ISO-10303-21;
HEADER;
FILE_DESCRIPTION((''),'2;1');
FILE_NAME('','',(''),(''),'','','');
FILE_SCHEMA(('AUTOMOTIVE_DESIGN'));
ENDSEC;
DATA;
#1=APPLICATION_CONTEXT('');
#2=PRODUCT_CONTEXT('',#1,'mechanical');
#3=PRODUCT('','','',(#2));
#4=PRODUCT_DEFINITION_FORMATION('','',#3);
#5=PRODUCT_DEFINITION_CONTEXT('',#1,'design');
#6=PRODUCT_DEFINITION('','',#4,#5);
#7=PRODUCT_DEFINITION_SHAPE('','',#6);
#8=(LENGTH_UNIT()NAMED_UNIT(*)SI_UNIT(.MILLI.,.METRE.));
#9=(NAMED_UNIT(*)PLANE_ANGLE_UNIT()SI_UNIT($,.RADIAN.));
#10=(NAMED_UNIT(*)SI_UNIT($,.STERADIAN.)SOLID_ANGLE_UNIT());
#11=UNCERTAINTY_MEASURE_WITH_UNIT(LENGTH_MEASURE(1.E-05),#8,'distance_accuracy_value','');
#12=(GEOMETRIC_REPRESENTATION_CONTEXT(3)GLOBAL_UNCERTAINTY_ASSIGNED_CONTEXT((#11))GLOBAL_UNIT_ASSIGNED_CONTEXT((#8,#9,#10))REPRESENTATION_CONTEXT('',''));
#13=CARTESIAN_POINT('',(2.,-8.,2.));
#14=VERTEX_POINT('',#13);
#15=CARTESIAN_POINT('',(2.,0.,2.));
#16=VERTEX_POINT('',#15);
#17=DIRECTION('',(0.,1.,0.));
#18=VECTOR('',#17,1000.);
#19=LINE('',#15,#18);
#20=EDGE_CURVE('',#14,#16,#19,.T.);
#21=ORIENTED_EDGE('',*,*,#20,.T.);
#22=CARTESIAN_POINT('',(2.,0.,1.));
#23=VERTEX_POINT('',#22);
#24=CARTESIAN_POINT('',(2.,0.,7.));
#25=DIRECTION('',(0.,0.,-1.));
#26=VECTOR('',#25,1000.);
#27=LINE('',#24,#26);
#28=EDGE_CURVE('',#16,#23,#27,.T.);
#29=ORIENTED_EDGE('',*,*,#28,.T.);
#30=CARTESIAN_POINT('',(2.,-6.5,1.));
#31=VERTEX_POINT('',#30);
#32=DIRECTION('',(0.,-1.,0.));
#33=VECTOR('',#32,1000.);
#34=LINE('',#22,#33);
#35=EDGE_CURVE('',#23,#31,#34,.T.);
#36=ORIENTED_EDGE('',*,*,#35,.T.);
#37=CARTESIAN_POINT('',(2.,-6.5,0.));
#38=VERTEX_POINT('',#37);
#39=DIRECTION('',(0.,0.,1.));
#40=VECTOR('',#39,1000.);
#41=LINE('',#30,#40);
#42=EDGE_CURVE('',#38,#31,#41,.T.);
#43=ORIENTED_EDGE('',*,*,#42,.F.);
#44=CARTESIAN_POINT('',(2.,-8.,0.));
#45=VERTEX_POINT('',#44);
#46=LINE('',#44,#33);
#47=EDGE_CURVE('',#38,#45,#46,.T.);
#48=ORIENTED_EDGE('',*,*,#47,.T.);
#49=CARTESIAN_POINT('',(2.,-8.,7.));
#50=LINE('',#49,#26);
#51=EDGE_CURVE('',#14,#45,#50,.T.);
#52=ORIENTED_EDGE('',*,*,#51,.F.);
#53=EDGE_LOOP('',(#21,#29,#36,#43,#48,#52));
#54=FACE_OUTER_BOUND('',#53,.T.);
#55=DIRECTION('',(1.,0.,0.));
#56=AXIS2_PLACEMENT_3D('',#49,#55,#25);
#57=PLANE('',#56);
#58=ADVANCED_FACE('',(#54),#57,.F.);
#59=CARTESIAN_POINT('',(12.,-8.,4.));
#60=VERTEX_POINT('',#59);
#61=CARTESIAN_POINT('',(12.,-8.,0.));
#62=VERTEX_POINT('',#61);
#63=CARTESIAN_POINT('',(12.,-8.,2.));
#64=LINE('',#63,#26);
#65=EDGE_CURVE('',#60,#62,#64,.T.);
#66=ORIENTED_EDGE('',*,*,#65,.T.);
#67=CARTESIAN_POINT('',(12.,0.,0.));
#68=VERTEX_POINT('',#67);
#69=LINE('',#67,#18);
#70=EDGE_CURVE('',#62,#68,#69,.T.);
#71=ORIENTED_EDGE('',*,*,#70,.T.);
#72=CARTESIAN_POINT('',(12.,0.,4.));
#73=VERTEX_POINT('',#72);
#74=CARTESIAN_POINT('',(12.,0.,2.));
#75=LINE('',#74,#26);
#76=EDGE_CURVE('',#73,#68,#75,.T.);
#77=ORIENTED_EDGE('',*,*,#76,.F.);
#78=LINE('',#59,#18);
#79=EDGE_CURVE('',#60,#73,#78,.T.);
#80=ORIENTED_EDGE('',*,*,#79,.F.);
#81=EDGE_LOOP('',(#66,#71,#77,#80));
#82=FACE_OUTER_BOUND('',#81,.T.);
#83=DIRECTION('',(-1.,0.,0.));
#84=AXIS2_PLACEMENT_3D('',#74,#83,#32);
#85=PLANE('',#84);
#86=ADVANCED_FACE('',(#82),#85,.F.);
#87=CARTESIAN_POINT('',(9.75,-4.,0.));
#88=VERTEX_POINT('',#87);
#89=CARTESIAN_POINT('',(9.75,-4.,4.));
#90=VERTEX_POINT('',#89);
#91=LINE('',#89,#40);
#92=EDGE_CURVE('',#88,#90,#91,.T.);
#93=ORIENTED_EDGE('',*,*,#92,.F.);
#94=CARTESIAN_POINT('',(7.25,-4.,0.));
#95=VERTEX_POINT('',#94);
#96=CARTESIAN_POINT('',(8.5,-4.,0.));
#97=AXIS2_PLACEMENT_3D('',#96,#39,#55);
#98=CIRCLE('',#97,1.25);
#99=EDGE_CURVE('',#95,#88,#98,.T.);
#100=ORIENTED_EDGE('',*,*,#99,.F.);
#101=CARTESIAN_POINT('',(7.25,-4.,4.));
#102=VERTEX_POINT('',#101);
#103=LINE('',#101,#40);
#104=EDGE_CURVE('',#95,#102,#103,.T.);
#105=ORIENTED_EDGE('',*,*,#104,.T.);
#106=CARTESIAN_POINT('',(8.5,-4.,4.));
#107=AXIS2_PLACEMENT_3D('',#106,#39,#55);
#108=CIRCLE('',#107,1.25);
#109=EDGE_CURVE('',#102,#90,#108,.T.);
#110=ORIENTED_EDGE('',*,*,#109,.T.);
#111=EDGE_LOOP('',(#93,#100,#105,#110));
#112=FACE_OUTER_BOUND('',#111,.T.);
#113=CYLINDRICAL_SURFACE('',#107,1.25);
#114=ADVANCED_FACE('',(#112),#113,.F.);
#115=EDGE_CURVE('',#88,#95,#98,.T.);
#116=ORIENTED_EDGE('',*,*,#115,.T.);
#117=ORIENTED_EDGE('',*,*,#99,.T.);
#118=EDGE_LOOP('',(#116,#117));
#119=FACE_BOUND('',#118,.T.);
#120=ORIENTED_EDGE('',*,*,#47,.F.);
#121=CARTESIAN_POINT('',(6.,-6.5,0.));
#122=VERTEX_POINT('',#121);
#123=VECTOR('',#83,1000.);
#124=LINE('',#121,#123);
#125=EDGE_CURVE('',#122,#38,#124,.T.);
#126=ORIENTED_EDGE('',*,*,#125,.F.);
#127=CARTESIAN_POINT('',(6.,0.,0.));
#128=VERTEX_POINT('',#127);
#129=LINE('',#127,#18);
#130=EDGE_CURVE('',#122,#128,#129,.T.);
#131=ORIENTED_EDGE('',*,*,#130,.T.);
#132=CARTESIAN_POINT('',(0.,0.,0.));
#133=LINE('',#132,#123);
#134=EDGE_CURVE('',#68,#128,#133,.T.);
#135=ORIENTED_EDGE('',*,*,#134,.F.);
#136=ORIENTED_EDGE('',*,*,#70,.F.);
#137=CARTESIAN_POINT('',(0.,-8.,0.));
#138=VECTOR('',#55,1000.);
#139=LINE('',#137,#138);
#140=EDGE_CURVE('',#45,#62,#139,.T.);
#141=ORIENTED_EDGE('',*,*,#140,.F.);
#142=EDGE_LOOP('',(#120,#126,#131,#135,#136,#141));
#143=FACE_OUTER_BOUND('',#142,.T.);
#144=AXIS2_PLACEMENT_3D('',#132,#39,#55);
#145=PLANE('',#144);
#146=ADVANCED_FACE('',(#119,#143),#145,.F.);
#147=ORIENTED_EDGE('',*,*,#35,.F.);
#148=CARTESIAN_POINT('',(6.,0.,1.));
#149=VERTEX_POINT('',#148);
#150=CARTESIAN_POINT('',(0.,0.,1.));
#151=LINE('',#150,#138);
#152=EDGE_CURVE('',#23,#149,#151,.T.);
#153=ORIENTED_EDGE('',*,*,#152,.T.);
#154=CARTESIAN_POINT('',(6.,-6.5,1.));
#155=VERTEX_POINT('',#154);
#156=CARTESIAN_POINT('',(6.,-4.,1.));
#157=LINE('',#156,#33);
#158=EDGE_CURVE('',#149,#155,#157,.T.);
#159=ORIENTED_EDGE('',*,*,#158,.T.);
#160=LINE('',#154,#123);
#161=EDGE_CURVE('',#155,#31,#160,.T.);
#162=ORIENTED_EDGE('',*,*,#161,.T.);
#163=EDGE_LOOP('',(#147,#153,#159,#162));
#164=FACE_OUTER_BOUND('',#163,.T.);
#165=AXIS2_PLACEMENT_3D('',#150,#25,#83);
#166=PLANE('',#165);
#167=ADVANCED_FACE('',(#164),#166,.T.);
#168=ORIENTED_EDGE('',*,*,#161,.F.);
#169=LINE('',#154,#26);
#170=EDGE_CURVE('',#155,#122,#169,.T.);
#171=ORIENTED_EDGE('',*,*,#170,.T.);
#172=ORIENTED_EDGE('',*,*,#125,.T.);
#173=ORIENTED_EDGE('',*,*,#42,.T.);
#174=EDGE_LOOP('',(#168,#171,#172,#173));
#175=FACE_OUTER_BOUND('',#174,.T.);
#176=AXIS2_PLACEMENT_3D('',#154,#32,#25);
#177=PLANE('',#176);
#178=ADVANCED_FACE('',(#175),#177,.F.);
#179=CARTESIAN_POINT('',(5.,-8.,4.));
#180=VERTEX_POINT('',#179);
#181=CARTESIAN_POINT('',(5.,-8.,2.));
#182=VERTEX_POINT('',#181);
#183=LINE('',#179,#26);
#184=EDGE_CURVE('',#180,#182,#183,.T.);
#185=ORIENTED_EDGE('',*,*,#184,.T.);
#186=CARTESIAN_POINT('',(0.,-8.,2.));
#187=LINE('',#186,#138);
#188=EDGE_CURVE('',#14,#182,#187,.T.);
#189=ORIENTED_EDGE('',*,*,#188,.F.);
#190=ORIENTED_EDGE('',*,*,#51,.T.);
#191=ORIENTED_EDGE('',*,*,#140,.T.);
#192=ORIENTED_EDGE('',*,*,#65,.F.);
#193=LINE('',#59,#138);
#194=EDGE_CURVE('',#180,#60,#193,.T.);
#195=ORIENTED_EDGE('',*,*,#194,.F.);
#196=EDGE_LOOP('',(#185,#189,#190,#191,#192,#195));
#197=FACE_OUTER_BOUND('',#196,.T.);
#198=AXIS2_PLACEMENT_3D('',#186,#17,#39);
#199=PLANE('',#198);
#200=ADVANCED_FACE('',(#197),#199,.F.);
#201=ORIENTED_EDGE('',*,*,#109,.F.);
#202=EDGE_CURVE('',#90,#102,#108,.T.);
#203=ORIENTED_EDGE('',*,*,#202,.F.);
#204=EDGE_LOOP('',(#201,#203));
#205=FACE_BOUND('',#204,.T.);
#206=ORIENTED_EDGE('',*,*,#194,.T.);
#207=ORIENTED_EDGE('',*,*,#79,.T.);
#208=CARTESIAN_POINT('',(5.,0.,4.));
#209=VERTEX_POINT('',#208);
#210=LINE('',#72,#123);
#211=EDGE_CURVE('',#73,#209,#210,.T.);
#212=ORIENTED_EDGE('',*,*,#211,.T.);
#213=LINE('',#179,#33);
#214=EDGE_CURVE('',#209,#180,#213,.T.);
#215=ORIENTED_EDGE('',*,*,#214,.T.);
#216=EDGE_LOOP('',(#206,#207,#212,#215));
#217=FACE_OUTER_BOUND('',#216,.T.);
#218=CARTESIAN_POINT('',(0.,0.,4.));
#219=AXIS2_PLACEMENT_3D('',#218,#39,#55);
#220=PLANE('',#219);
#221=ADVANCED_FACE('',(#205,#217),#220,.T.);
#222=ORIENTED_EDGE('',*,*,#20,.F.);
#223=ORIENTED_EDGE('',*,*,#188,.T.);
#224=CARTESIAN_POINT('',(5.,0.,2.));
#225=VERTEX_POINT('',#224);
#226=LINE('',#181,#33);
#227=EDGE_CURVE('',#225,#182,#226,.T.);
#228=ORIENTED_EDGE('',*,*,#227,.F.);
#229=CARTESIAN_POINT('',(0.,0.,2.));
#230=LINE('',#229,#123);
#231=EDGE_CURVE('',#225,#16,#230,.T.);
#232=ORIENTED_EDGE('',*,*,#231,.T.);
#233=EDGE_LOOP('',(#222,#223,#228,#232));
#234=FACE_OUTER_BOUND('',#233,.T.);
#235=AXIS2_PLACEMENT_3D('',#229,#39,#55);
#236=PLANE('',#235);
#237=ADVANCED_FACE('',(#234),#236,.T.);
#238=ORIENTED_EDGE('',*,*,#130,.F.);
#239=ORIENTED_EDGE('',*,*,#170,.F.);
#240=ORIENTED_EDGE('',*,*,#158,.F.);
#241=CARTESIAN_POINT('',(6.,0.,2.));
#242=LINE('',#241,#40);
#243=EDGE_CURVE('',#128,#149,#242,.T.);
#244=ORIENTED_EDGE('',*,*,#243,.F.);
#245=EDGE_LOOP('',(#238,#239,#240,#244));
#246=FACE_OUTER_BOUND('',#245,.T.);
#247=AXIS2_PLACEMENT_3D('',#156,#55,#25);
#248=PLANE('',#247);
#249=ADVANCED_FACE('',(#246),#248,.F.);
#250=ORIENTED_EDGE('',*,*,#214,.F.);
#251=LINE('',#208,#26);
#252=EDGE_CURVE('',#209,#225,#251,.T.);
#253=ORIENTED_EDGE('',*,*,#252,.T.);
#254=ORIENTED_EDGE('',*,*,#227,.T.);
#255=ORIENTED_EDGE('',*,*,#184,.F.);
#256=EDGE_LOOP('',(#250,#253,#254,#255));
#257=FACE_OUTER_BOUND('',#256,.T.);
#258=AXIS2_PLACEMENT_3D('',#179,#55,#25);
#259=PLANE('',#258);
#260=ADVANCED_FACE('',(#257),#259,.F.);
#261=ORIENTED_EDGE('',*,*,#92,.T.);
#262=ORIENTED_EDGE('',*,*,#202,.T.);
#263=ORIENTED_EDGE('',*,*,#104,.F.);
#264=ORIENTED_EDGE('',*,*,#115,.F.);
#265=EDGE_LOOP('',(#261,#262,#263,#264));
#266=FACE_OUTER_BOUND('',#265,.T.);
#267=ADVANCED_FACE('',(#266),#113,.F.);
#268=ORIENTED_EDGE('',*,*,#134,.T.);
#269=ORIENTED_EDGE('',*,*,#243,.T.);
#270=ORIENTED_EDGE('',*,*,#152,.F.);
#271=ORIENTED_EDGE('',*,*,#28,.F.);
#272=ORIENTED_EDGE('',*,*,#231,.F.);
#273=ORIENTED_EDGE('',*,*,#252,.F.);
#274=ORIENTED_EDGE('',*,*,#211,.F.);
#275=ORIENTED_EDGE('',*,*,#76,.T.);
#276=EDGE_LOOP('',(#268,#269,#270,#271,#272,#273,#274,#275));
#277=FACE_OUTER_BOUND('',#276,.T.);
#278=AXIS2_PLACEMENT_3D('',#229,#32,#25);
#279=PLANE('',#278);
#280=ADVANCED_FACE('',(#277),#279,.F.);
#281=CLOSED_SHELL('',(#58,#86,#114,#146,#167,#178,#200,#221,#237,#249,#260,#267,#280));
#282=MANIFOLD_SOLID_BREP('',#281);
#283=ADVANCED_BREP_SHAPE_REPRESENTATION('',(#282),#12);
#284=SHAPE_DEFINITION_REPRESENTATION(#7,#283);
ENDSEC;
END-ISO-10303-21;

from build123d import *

# Parameters (mm, degrees)
SKETCH1_W             = 12
SKETCH1_H             = 8
BOSS_EXTRUDE1_DEPTH   = 2
SKETCH2_W             = 7
SKETCH2_H             = 8
BOSS_EXTRUDE2_DEPTH   = 2
SKETCH3_R             = 1.25
CUT_EXTRUDE1_DEPTH    = 10
CUT_EXTRUDE2_DEPTH    = 1
SKETCH5_W             = 2
SKETCH5_H             = 8
CUT_EXTRUDE3_DEPTH    = 7
MOVE_FACE1_BY         = 0.5
M3_TAPPED_HOLE4_D     = 2.5
M3_TAPPED_HOLE4_DEPTH = 7.5
M3_TAPPED_HOLE4_TIP   = 0.751075774


with BuildPart() as part:
    # Sketch1 → Boss-Extrude1 (new body)
    with BuildSketch(Plane.XY):
        with Locations((6, -4)):
            Rectangle(SKETCH1_W, SKETCH1_H)
    extrude(amount=BOSS_EXTRUDE1_DEPTH)

    # Sketch2 → Boss-Extrude2 (add)
    with BuildSketch(Plane.XY.offset(2)):
        with Locations((8.5, -4)):
            Rectangle(SKETCH2_W, SKETCH2_H)
    extrude(amount=BOSS_EXTRUDE2_DEPTH)

    # Sketch3 → Cut-Extrude1 (cut)
    with BuildSketch(Plane.XY.offset(4)):
        with Locations((8.5, -4)):
            Circle(SKETCH3_R)
    extrude(amount=-CUT_EXTRUDE1_DEPTH, mode=Mode.SUBTRACT)

    # Sketch4 → Cut-Extrude2 (cut)
    with BuildSketch(Plane(origin=(0, 0, 0), x_dir=(-1, 0, 0), z_dir=(0, 0, -1))):
        Polygon((0, -4), (0, 1.17366925), (-6, 1.17366925), (-6, -4), (-6, -6.5), (0, -6.5), align=None)
    extrude(amount=-CUT_EXTRUDE2_DEPTH, mode=Mode.SUBTRACT)

    # Sketch5 → Cut-Extrude3 (cut)
    with BuildSketch(Plane(origin=(0, 0, 0), x_dir=(-1, 0, 0), z_dir=(0, 0, -1))):
        with Locations((-1, -4)):
            Rectangle(SKETCH5_W, SKETCH5_H)
    extrude(amount=-CUT_EXTRUDE3_DEPTH, mode=Mode.SUBTRACT)

    # Move Face1: a curved face moved outward by 0.5
    add(Solid.thicken(part.faces().sort_by_distance((7.25, -4, 2))[0], MOVE_FACE1_BY))

    # M3 Tapped Hole4
    with Locations(Plane.XY.offset(4)):
        with Locations((8.5, -4)):
            Hole(M3_TAPPED_HOLE4_D / 2, depth=M3_TAPPED_HOLE4_DEPTH)
            with Locations((0, 0, -(M3_TAPPED_HOLE4_DEPTH + M3_TAPPED_HOLE4_TIP / 2))):  # 118° drill point
                Cone(0, M3_TAPPED_HOLE4_D / 2, M3_TAPPED_HOLE4_TIP, mode=Mode.SUBTRACT)


solid = part.part
